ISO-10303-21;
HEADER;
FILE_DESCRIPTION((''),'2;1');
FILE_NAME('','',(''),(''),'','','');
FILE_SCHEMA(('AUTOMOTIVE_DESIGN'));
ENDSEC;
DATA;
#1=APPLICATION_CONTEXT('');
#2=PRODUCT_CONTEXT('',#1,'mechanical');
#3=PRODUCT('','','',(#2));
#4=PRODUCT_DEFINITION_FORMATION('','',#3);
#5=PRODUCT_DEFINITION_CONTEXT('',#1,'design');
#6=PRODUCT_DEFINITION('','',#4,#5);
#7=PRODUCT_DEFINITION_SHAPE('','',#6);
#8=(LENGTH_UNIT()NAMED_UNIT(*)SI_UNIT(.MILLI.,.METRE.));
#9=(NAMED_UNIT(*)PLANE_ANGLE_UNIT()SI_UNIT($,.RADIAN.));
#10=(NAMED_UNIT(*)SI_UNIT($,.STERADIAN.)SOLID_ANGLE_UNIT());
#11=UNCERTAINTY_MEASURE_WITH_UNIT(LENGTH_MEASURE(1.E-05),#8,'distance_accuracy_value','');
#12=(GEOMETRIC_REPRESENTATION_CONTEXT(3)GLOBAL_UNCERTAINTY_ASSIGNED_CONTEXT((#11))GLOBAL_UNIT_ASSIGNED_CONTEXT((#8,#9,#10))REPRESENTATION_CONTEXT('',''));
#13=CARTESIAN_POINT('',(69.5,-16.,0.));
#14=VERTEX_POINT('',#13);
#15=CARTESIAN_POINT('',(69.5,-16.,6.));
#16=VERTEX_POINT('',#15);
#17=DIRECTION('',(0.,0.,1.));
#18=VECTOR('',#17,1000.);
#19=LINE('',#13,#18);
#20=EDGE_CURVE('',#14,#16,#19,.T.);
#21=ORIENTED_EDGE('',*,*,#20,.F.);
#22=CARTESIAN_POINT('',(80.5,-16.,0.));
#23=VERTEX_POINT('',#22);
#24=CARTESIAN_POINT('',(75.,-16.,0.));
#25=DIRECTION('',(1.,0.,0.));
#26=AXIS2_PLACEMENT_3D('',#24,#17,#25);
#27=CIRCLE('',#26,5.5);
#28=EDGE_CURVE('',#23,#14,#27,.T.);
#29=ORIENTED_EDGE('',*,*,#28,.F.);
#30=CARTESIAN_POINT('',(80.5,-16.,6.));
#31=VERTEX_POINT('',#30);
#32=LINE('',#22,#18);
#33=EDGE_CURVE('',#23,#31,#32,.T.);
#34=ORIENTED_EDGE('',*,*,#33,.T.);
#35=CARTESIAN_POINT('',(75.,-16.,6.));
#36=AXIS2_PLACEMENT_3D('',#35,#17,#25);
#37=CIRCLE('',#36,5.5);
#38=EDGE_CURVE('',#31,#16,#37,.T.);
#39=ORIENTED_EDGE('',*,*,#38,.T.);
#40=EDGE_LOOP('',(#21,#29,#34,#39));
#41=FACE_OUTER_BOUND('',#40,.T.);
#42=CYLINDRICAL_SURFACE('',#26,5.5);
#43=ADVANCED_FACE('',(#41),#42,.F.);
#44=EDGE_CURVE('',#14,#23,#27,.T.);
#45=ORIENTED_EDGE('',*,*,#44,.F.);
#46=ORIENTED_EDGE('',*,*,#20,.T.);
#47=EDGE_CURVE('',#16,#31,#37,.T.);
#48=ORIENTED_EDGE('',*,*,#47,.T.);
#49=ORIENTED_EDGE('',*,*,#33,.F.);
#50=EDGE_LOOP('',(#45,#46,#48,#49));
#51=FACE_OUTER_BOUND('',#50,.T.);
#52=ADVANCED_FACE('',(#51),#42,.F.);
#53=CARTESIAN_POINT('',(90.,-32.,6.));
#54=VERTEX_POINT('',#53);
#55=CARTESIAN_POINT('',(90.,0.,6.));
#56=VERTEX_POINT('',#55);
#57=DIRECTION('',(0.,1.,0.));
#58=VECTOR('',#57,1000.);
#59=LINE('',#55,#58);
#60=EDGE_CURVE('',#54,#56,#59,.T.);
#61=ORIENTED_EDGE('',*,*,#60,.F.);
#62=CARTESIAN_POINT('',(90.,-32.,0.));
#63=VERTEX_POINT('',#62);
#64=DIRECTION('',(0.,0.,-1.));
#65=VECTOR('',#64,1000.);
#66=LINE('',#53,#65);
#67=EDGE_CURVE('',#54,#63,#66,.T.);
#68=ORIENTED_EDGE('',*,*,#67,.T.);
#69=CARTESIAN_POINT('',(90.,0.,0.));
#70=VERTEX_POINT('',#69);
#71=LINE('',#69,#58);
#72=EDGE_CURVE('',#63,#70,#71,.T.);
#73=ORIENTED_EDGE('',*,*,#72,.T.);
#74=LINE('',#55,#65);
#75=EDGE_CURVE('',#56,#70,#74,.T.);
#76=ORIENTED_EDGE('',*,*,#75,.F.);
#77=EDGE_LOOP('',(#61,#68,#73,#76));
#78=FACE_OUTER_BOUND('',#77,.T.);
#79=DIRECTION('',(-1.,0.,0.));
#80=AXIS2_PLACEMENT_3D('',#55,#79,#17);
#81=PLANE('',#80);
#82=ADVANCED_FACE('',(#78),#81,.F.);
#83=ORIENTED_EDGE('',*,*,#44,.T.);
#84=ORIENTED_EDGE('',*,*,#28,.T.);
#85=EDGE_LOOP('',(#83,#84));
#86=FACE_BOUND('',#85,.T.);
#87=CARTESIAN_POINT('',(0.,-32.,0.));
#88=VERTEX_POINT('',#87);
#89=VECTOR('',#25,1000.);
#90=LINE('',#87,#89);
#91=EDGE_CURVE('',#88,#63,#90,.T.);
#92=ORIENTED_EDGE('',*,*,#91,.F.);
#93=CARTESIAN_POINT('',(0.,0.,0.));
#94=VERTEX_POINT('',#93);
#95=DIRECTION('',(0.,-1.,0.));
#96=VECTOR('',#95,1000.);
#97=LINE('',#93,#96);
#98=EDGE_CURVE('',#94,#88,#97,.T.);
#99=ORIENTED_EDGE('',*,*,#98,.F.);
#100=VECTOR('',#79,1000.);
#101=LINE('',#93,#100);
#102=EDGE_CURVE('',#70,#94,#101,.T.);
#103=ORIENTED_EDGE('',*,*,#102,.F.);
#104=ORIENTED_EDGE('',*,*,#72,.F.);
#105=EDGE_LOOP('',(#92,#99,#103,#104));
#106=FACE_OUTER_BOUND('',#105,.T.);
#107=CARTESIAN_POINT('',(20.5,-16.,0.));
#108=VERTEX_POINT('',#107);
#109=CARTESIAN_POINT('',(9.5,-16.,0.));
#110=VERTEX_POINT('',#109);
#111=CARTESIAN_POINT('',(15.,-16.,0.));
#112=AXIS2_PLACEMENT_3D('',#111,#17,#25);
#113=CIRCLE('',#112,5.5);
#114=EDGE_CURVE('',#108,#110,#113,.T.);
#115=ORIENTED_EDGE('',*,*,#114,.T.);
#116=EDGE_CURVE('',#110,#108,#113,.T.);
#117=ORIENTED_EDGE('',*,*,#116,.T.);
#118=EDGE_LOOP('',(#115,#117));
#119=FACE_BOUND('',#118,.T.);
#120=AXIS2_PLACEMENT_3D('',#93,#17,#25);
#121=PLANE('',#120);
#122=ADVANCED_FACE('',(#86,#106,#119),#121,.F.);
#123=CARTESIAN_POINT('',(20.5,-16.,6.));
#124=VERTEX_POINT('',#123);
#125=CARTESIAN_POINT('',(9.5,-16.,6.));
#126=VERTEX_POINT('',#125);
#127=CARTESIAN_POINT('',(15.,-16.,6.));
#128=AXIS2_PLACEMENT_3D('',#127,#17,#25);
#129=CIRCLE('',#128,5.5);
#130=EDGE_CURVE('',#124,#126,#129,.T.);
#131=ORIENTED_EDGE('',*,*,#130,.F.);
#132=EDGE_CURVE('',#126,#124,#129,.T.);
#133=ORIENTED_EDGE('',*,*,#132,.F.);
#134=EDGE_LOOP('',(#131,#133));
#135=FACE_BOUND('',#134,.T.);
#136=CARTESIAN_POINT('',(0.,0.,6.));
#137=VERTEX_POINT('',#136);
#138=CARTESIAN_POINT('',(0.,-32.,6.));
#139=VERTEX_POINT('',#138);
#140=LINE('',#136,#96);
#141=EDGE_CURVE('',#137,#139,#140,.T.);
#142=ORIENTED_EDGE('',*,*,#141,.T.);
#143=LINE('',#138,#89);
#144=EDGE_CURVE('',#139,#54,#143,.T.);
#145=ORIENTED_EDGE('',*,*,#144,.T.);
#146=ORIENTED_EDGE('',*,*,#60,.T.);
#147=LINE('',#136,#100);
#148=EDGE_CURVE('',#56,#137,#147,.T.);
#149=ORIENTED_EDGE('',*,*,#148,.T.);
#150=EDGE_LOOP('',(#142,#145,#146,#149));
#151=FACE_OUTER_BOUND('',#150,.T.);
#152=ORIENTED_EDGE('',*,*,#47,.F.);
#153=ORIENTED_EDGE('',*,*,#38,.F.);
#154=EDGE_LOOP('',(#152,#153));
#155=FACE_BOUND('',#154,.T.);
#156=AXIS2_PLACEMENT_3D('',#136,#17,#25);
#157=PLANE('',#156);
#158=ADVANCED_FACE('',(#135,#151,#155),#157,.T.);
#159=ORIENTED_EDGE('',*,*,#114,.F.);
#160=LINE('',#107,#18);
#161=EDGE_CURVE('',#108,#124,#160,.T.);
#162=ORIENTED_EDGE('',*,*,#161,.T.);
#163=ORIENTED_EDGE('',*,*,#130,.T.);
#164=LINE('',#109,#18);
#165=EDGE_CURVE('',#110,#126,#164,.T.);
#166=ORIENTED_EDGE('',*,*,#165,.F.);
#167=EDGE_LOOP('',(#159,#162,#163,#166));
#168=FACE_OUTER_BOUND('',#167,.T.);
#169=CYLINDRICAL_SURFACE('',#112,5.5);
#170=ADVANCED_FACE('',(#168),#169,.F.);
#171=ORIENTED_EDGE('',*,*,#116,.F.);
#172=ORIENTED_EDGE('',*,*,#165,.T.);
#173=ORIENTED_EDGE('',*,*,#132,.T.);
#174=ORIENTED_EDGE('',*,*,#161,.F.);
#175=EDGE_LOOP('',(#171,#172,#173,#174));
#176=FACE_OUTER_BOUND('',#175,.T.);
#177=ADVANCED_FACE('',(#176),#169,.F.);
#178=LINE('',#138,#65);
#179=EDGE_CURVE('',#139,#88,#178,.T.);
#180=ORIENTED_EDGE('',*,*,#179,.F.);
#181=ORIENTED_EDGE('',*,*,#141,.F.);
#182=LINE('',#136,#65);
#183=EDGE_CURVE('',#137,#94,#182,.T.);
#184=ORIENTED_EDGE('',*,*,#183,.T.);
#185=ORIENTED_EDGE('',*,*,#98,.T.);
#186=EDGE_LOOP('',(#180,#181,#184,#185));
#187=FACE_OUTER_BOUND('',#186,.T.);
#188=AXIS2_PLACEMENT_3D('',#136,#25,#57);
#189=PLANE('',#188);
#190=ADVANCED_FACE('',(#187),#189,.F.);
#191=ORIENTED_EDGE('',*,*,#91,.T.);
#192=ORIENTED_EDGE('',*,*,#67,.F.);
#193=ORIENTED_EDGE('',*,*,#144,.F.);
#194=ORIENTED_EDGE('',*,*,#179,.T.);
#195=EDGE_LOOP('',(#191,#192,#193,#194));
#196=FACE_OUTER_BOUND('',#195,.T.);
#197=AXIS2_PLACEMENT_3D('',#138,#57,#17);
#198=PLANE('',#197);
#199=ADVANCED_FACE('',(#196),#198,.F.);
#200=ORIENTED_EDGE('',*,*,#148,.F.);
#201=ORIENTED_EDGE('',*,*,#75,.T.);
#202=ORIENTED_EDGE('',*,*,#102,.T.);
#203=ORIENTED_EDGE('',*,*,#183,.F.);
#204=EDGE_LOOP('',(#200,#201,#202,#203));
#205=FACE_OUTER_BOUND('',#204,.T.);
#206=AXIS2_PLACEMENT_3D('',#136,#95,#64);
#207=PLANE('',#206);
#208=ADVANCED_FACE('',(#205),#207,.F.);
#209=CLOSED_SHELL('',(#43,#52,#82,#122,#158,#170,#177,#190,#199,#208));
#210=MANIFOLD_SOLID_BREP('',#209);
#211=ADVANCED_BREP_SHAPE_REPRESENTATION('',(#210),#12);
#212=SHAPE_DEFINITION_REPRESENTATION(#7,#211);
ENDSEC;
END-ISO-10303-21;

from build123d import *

# Parameters (mm, degrees)
SKETCH1_W           = 90
SKETCH1_H           = 32
BOSS_EXTRUDE1_DEPTH = 6
SKETCH2_R           = 5.5
CUT_EXTRUDE1_DEPTH  = 6
LPATTERN1_COUNT     = 2
LPATTERN1_PITCH     = 60


with BuildPart() as part:
    # Sketch1 → Boss-Extrude1 (new body)
    with BuildSketch(Plane.XY):
        with Locations((45, -16)):
            Rectangle(SKETCH1_W, SKETCH1_H)
    extrude(amount=BOSS_EXTRUDE1_DEPTH)

    # Sketch2 → Cut-Extrude1 (cut)
    with BuildSketch(Plane.XY.offset(6)):
        with Locations((15, -16)):
            Circle(SKETCH2_R)
    cut_extrude1 = extrude(amount=-CUT_EXTRUDE1_DEPTH, mode=Mode.SUBTRACT)

    # LPattern1: Cut-Extrude1 ×2
    with Locations(*[(i * LPATTERN1_PITCH, 0, 0) for i in range(1, LPATTERN1_COUNT)]):
        add(cut_extrude1, mode=Mode.SUBTRACT)


solid = part.part
